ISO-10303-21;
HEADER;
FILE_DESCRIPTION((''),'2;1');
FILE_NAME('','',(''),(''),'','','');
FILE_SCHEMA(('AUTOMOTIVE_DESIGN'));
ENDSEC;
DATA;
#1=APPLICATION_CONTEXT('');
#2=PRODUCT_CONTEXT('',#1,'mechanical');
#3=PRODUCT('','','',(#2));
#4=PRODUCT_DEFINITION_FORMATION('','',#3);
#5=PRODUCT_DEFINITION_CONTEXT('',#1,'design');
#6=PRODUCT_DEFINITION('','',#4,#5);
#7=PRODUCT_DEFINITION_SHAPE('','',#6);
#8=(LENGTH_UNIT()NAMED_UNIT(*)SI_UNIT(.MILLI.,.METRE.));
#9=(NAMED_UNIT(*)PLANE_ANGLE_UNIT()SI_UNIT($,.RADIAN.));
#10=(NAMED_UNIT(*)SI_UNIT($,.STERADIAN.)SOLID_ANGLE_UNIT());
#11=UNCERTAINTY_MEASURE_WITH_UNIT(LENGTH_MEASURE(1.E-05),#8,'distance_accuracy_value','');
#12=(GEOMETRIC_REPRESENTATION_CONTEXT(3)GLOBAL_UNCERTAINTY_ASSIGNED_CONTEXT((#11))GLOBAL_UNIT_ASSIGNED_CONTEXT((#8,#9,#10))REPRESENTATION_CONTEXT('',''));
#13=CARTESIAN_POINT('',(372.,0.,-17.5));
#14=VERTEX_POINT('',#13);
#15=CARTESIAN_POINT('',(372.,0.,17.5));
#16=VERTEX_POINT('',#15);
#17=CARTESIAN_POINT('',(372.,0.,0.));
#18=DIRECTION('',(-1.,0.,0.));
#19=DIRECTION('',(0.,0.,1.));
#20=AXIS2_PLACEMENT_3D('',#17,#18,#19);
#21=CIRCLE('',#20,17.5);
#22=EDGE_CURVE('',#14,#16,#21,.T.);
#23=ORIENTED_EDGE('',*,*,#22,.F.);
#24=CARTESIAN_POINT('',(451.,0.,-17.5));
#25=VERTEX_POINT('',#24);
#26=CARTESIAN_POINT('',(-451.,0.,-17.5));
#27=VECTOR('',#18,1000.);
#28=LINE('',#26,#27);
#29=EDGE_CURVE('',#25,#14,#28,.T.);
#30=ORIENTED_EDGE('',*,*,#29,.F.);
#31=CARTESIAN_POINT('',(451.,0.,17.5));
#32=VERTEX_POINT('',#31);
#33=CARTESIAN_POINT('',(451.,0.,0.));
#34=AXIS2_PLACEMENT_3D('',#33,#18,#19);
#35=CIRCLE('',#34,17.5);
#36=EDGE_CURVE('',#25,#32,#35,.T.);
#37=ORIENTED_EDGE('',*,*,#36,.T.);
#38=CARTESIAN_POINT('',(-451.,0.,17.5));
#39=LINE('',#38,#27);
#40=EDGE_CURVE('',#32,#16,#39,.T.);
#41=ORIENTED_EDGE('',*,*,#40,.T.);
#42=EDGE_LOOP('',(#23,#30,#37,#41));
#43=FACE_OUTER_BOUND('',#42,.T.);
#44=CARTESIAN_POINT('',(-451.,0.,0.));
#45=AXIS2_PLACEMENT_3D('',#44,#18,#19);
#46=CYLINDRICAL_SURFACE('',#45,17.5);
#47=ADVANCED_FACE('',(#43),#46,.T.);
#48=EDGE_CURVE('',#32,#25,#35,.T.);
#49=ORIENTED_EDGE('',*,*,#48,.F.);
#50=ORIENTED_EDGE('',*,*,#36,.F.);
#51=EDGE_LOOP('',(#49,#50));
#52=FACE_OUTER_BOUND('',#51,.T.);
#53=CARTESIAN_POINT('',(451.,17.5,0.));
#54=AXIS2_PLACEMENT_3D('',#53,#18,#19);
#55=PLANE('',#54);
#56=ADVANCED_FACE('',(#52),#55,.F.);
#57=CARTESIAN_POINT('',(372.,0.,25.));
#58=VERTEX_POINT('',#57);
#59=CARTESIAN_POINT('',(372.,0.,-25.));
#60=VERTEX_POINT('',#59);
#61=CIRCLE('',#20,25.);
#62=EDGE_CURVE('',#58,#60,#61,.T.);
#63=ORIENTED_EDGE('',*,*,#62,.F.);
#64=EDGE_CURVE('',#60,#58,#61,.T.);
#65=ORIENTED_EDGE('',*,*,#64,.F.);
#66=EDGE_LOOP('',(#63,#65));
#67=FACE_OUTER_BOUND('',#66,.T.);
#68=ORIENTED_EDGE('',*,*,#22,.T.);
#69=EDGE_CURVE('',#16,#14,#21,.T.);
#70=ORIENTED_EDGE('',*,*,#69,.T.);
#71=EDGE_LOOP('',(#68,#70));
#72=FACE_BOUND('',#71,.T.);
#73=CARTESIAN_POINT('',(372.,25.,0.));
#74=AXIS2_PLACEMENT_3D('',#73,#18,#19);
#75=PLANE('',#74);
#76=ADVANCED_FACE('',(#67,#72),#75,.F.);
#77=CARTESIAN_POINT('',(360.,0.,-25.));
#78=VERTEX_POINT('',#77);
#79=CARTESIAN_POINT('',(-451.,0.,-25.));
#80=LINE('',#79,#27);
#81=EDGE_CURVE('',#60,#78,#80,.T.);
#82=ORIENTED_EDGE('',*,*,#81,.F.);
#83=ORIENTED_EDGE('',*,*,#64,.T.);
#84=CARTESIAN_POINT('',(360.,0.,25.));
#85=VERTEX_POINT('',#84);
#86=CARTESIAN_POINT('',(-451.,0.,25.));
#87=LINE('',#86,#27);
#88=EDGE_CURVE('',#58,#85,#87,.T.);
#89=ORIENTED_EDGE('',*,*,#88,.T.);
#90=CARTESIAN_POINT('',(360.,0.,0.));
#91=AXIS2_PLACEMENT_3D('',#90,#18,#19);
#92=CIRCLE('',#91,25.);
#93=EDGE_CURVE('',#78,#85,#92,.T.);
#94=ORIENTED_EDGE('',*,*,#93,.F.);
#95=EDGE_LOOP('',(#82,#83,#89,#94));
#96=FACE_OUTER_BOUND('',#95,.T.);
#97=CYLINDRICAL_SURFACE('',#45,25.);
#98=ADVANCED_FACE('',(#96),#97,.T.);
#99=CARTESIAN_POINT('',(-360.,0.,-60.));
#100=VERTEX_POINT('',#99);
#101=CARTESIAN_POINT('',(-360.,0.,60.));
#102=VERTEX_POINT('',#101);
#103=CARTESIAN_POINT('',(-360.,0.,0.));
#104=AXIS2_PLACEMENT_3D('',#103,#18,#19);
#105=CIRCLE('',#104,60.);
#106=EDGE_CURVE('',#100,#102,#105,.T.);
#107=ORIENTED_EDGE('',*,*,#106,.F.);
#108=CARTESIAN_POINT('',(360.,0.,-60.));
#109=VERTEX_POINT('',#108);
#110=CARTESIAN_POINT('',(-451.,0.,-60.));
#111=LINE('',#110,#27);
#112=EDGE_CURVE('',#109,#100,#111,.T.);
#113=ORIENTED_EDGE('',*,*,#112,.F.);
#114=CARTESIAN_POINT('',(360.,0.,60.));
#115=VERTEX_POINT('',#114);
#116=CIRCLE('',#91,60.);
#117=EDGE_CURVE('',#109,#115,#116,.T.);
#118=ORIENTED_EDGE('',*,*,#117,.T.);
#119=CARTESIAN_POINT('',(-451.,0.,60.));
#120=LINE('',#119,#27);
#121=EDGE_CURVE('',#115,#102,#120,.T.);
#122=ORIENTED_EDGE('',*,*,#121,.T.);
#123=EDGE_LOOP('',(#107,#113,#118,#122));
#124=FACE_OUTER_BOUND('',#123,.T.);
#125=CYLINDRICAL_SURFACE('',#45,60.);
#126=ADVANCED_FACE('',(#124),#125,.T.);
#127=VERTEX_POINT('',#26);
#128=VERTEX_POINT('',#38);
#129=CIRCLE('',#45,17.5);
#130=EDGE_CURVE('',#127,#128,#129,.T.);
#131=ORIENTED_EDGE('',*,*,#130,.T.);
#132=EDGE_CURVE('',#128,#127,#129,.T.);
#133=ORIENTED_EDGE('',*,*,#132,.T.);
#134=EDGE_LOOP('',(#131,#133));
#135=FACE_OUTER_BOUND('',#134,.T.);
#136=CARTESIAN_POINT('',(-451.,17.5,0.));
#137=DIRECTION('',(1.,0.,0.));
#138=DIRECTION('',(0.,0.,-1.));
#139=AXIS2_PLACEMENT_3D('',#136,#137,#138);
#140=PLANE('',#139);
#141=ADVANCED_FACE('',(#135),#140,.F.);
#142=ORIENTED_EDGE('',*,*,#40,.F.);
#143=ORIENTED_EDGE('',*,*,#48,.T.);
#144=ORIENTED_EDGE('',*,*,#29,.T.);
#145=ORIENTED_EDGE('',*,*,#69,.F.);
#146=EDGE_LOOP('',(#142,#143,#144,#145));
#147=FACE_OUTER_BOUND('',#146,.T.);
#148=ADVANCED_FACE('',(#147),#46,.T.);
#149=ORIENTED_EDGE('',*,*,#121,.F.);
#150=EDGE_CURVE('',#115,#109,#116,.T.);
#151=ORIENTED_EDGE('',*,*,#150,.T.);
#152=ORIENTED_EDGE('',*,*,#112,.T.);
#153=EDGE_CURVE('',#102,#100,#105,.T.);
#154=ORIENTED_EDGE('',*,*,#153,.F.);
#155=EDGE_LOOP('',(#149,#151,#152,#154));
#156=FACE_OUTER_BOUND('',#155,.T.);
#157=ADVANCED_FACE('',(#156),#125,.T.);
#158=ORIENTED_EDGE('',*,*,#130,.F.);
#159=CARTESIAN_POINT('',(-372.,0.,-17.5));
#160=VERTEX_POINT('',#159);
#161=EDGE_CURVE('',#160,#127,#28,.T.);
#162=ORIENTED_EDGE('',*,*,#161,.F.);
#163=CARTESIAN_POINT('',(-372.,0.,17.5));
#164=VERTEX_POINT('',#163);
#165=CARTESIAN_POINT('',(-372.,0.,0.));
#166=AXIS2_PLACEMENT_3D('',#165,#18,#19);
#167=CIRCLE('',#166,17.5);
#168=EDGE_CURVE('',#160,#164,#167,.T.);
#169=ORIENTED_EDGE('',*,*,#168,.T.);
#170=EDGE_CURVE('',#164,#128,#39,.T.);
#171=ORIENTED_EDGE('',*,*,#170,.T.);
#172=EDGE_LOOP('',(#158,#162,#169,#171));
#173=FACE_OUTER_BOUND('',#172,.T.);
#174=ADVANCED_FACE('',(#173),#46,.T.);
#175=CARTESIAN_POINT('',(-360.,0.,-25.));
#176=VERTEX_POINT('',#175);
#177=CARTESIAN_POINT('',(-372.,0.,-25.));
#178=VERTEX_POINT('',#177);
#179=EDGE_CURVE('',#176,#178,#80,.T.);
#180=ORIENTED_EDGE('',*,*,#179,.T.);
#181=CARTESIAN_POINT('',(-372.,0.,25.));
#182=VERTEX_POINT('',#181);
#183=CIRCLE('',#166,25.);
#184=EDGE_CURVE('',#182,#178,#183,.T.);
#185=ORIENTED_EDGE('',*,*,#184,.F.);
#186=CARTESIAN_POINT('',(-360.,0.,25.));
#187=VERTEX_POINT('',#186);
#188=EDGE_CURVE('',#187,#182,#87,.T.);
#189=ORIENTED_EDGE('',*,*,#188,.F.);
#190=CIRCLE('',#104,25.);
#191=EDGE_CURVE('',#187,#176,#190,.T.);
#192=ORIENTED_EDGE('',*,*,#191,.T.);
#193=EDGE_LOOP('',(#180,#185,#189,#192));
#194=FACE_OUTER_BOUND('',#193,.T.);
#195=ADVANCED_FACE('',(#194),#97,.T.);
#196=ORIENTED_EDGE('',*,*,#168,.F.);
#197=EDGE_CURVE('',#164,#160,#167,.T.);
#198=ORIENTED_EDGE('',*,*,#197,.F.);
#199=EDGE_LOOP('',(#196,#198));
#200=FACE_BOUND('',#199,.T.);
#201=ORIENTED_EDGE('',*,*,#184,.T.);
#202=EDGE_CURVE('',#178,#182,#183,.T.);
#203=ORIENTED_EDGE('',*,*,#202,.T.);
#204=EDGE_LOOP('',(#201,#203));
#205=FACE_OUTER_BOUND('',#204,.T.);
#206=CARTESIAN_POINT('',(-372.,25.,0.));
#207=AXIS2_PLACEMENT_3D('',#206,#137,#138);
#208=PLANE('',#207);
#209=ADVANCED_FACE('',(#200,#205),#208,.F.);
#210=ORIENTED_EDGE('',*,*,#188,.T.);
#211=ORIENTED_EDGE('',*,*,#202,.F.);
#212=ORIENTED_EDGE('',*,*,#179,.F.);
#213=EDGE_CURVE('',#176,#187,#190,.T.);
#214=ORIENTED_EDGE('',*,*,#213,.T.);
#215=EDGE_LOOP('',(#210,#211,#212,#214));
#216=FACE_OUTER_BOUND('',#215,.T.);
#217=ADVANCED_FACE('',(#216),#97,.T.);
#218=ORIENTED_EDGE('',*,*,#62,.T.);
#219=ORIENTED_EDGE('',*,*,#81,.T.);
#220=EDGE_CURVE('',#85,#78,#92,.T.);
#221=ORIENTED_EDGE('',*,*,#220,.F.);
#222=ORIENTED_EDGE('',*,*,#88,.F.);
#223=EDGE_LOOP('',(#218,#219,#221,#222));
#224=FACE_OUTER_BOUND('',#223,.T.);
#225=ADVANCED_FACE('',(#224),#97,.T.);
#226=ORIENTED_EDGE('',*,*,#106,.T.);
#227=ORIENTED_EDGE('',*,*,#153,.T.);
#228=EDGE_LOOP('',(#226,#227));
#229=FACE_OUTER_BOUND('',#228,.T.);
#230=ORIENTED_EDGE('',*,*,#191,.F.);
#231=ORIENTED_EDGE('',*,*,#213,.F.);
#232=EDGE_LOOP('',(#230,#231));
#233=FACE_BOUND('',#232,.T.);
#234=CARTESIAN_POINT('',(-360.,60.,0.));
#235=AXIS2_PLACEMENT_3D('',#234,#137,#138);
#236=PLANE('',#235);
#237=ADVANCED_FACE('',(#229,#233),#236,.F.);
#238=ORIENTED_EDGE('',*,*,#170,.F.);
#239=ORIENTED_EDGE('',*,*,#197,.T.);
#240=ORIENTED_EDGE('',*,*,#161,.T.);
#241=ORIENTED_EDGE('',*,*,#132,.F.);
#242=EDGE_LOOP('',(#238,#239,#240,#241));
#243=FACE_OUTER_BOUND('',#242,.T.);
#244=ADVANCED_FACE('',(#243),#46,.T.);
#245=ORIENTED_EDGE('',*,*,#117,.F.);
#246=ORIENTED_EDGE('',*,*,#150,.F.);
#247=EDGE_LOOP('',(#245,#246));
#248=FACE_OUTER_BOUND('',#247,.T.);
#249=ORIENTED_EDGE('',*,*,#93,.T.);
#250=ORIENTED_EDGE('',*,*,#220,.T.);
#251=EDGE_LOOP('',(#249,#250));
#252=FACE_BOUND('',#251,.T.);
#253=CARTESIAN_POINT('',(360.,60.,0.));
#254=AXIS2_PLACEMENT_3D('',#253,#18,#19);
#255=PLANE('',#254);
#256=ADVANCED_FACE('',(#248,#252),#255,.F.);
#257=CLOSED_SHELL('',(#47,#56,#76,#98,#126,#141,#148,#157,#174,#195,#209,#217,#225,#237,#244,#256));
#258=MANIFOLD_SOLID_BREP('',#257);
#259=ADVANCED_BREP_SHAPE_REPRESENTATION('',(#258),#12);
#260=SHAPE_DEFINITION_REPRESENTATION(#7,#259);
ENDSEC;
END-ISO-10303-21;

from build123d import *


with BuildPart() as part:
    # 草图1 → 旋转1 (revolve)
    with BuildSketch(Plane.XY, mode=Mode.PRIVATE) as revolve_1_sk:
        Polygon((-360, 60), (360, 60), (360, 25), (372, 25), (372, 17.5), (451, 17.5), (451, 0), (-451, 0), (-451, 17.5), (-372, 17.5), (-372, 25), (-360, 25), align=None)
    revolve(revolve_1_sk.sketch.rotate(Axis((-451, 0, 0), (1, 0, 0)), 90), axis=Axis((-451, 0, 0), (1, 0, 0)))


solid = part.part
